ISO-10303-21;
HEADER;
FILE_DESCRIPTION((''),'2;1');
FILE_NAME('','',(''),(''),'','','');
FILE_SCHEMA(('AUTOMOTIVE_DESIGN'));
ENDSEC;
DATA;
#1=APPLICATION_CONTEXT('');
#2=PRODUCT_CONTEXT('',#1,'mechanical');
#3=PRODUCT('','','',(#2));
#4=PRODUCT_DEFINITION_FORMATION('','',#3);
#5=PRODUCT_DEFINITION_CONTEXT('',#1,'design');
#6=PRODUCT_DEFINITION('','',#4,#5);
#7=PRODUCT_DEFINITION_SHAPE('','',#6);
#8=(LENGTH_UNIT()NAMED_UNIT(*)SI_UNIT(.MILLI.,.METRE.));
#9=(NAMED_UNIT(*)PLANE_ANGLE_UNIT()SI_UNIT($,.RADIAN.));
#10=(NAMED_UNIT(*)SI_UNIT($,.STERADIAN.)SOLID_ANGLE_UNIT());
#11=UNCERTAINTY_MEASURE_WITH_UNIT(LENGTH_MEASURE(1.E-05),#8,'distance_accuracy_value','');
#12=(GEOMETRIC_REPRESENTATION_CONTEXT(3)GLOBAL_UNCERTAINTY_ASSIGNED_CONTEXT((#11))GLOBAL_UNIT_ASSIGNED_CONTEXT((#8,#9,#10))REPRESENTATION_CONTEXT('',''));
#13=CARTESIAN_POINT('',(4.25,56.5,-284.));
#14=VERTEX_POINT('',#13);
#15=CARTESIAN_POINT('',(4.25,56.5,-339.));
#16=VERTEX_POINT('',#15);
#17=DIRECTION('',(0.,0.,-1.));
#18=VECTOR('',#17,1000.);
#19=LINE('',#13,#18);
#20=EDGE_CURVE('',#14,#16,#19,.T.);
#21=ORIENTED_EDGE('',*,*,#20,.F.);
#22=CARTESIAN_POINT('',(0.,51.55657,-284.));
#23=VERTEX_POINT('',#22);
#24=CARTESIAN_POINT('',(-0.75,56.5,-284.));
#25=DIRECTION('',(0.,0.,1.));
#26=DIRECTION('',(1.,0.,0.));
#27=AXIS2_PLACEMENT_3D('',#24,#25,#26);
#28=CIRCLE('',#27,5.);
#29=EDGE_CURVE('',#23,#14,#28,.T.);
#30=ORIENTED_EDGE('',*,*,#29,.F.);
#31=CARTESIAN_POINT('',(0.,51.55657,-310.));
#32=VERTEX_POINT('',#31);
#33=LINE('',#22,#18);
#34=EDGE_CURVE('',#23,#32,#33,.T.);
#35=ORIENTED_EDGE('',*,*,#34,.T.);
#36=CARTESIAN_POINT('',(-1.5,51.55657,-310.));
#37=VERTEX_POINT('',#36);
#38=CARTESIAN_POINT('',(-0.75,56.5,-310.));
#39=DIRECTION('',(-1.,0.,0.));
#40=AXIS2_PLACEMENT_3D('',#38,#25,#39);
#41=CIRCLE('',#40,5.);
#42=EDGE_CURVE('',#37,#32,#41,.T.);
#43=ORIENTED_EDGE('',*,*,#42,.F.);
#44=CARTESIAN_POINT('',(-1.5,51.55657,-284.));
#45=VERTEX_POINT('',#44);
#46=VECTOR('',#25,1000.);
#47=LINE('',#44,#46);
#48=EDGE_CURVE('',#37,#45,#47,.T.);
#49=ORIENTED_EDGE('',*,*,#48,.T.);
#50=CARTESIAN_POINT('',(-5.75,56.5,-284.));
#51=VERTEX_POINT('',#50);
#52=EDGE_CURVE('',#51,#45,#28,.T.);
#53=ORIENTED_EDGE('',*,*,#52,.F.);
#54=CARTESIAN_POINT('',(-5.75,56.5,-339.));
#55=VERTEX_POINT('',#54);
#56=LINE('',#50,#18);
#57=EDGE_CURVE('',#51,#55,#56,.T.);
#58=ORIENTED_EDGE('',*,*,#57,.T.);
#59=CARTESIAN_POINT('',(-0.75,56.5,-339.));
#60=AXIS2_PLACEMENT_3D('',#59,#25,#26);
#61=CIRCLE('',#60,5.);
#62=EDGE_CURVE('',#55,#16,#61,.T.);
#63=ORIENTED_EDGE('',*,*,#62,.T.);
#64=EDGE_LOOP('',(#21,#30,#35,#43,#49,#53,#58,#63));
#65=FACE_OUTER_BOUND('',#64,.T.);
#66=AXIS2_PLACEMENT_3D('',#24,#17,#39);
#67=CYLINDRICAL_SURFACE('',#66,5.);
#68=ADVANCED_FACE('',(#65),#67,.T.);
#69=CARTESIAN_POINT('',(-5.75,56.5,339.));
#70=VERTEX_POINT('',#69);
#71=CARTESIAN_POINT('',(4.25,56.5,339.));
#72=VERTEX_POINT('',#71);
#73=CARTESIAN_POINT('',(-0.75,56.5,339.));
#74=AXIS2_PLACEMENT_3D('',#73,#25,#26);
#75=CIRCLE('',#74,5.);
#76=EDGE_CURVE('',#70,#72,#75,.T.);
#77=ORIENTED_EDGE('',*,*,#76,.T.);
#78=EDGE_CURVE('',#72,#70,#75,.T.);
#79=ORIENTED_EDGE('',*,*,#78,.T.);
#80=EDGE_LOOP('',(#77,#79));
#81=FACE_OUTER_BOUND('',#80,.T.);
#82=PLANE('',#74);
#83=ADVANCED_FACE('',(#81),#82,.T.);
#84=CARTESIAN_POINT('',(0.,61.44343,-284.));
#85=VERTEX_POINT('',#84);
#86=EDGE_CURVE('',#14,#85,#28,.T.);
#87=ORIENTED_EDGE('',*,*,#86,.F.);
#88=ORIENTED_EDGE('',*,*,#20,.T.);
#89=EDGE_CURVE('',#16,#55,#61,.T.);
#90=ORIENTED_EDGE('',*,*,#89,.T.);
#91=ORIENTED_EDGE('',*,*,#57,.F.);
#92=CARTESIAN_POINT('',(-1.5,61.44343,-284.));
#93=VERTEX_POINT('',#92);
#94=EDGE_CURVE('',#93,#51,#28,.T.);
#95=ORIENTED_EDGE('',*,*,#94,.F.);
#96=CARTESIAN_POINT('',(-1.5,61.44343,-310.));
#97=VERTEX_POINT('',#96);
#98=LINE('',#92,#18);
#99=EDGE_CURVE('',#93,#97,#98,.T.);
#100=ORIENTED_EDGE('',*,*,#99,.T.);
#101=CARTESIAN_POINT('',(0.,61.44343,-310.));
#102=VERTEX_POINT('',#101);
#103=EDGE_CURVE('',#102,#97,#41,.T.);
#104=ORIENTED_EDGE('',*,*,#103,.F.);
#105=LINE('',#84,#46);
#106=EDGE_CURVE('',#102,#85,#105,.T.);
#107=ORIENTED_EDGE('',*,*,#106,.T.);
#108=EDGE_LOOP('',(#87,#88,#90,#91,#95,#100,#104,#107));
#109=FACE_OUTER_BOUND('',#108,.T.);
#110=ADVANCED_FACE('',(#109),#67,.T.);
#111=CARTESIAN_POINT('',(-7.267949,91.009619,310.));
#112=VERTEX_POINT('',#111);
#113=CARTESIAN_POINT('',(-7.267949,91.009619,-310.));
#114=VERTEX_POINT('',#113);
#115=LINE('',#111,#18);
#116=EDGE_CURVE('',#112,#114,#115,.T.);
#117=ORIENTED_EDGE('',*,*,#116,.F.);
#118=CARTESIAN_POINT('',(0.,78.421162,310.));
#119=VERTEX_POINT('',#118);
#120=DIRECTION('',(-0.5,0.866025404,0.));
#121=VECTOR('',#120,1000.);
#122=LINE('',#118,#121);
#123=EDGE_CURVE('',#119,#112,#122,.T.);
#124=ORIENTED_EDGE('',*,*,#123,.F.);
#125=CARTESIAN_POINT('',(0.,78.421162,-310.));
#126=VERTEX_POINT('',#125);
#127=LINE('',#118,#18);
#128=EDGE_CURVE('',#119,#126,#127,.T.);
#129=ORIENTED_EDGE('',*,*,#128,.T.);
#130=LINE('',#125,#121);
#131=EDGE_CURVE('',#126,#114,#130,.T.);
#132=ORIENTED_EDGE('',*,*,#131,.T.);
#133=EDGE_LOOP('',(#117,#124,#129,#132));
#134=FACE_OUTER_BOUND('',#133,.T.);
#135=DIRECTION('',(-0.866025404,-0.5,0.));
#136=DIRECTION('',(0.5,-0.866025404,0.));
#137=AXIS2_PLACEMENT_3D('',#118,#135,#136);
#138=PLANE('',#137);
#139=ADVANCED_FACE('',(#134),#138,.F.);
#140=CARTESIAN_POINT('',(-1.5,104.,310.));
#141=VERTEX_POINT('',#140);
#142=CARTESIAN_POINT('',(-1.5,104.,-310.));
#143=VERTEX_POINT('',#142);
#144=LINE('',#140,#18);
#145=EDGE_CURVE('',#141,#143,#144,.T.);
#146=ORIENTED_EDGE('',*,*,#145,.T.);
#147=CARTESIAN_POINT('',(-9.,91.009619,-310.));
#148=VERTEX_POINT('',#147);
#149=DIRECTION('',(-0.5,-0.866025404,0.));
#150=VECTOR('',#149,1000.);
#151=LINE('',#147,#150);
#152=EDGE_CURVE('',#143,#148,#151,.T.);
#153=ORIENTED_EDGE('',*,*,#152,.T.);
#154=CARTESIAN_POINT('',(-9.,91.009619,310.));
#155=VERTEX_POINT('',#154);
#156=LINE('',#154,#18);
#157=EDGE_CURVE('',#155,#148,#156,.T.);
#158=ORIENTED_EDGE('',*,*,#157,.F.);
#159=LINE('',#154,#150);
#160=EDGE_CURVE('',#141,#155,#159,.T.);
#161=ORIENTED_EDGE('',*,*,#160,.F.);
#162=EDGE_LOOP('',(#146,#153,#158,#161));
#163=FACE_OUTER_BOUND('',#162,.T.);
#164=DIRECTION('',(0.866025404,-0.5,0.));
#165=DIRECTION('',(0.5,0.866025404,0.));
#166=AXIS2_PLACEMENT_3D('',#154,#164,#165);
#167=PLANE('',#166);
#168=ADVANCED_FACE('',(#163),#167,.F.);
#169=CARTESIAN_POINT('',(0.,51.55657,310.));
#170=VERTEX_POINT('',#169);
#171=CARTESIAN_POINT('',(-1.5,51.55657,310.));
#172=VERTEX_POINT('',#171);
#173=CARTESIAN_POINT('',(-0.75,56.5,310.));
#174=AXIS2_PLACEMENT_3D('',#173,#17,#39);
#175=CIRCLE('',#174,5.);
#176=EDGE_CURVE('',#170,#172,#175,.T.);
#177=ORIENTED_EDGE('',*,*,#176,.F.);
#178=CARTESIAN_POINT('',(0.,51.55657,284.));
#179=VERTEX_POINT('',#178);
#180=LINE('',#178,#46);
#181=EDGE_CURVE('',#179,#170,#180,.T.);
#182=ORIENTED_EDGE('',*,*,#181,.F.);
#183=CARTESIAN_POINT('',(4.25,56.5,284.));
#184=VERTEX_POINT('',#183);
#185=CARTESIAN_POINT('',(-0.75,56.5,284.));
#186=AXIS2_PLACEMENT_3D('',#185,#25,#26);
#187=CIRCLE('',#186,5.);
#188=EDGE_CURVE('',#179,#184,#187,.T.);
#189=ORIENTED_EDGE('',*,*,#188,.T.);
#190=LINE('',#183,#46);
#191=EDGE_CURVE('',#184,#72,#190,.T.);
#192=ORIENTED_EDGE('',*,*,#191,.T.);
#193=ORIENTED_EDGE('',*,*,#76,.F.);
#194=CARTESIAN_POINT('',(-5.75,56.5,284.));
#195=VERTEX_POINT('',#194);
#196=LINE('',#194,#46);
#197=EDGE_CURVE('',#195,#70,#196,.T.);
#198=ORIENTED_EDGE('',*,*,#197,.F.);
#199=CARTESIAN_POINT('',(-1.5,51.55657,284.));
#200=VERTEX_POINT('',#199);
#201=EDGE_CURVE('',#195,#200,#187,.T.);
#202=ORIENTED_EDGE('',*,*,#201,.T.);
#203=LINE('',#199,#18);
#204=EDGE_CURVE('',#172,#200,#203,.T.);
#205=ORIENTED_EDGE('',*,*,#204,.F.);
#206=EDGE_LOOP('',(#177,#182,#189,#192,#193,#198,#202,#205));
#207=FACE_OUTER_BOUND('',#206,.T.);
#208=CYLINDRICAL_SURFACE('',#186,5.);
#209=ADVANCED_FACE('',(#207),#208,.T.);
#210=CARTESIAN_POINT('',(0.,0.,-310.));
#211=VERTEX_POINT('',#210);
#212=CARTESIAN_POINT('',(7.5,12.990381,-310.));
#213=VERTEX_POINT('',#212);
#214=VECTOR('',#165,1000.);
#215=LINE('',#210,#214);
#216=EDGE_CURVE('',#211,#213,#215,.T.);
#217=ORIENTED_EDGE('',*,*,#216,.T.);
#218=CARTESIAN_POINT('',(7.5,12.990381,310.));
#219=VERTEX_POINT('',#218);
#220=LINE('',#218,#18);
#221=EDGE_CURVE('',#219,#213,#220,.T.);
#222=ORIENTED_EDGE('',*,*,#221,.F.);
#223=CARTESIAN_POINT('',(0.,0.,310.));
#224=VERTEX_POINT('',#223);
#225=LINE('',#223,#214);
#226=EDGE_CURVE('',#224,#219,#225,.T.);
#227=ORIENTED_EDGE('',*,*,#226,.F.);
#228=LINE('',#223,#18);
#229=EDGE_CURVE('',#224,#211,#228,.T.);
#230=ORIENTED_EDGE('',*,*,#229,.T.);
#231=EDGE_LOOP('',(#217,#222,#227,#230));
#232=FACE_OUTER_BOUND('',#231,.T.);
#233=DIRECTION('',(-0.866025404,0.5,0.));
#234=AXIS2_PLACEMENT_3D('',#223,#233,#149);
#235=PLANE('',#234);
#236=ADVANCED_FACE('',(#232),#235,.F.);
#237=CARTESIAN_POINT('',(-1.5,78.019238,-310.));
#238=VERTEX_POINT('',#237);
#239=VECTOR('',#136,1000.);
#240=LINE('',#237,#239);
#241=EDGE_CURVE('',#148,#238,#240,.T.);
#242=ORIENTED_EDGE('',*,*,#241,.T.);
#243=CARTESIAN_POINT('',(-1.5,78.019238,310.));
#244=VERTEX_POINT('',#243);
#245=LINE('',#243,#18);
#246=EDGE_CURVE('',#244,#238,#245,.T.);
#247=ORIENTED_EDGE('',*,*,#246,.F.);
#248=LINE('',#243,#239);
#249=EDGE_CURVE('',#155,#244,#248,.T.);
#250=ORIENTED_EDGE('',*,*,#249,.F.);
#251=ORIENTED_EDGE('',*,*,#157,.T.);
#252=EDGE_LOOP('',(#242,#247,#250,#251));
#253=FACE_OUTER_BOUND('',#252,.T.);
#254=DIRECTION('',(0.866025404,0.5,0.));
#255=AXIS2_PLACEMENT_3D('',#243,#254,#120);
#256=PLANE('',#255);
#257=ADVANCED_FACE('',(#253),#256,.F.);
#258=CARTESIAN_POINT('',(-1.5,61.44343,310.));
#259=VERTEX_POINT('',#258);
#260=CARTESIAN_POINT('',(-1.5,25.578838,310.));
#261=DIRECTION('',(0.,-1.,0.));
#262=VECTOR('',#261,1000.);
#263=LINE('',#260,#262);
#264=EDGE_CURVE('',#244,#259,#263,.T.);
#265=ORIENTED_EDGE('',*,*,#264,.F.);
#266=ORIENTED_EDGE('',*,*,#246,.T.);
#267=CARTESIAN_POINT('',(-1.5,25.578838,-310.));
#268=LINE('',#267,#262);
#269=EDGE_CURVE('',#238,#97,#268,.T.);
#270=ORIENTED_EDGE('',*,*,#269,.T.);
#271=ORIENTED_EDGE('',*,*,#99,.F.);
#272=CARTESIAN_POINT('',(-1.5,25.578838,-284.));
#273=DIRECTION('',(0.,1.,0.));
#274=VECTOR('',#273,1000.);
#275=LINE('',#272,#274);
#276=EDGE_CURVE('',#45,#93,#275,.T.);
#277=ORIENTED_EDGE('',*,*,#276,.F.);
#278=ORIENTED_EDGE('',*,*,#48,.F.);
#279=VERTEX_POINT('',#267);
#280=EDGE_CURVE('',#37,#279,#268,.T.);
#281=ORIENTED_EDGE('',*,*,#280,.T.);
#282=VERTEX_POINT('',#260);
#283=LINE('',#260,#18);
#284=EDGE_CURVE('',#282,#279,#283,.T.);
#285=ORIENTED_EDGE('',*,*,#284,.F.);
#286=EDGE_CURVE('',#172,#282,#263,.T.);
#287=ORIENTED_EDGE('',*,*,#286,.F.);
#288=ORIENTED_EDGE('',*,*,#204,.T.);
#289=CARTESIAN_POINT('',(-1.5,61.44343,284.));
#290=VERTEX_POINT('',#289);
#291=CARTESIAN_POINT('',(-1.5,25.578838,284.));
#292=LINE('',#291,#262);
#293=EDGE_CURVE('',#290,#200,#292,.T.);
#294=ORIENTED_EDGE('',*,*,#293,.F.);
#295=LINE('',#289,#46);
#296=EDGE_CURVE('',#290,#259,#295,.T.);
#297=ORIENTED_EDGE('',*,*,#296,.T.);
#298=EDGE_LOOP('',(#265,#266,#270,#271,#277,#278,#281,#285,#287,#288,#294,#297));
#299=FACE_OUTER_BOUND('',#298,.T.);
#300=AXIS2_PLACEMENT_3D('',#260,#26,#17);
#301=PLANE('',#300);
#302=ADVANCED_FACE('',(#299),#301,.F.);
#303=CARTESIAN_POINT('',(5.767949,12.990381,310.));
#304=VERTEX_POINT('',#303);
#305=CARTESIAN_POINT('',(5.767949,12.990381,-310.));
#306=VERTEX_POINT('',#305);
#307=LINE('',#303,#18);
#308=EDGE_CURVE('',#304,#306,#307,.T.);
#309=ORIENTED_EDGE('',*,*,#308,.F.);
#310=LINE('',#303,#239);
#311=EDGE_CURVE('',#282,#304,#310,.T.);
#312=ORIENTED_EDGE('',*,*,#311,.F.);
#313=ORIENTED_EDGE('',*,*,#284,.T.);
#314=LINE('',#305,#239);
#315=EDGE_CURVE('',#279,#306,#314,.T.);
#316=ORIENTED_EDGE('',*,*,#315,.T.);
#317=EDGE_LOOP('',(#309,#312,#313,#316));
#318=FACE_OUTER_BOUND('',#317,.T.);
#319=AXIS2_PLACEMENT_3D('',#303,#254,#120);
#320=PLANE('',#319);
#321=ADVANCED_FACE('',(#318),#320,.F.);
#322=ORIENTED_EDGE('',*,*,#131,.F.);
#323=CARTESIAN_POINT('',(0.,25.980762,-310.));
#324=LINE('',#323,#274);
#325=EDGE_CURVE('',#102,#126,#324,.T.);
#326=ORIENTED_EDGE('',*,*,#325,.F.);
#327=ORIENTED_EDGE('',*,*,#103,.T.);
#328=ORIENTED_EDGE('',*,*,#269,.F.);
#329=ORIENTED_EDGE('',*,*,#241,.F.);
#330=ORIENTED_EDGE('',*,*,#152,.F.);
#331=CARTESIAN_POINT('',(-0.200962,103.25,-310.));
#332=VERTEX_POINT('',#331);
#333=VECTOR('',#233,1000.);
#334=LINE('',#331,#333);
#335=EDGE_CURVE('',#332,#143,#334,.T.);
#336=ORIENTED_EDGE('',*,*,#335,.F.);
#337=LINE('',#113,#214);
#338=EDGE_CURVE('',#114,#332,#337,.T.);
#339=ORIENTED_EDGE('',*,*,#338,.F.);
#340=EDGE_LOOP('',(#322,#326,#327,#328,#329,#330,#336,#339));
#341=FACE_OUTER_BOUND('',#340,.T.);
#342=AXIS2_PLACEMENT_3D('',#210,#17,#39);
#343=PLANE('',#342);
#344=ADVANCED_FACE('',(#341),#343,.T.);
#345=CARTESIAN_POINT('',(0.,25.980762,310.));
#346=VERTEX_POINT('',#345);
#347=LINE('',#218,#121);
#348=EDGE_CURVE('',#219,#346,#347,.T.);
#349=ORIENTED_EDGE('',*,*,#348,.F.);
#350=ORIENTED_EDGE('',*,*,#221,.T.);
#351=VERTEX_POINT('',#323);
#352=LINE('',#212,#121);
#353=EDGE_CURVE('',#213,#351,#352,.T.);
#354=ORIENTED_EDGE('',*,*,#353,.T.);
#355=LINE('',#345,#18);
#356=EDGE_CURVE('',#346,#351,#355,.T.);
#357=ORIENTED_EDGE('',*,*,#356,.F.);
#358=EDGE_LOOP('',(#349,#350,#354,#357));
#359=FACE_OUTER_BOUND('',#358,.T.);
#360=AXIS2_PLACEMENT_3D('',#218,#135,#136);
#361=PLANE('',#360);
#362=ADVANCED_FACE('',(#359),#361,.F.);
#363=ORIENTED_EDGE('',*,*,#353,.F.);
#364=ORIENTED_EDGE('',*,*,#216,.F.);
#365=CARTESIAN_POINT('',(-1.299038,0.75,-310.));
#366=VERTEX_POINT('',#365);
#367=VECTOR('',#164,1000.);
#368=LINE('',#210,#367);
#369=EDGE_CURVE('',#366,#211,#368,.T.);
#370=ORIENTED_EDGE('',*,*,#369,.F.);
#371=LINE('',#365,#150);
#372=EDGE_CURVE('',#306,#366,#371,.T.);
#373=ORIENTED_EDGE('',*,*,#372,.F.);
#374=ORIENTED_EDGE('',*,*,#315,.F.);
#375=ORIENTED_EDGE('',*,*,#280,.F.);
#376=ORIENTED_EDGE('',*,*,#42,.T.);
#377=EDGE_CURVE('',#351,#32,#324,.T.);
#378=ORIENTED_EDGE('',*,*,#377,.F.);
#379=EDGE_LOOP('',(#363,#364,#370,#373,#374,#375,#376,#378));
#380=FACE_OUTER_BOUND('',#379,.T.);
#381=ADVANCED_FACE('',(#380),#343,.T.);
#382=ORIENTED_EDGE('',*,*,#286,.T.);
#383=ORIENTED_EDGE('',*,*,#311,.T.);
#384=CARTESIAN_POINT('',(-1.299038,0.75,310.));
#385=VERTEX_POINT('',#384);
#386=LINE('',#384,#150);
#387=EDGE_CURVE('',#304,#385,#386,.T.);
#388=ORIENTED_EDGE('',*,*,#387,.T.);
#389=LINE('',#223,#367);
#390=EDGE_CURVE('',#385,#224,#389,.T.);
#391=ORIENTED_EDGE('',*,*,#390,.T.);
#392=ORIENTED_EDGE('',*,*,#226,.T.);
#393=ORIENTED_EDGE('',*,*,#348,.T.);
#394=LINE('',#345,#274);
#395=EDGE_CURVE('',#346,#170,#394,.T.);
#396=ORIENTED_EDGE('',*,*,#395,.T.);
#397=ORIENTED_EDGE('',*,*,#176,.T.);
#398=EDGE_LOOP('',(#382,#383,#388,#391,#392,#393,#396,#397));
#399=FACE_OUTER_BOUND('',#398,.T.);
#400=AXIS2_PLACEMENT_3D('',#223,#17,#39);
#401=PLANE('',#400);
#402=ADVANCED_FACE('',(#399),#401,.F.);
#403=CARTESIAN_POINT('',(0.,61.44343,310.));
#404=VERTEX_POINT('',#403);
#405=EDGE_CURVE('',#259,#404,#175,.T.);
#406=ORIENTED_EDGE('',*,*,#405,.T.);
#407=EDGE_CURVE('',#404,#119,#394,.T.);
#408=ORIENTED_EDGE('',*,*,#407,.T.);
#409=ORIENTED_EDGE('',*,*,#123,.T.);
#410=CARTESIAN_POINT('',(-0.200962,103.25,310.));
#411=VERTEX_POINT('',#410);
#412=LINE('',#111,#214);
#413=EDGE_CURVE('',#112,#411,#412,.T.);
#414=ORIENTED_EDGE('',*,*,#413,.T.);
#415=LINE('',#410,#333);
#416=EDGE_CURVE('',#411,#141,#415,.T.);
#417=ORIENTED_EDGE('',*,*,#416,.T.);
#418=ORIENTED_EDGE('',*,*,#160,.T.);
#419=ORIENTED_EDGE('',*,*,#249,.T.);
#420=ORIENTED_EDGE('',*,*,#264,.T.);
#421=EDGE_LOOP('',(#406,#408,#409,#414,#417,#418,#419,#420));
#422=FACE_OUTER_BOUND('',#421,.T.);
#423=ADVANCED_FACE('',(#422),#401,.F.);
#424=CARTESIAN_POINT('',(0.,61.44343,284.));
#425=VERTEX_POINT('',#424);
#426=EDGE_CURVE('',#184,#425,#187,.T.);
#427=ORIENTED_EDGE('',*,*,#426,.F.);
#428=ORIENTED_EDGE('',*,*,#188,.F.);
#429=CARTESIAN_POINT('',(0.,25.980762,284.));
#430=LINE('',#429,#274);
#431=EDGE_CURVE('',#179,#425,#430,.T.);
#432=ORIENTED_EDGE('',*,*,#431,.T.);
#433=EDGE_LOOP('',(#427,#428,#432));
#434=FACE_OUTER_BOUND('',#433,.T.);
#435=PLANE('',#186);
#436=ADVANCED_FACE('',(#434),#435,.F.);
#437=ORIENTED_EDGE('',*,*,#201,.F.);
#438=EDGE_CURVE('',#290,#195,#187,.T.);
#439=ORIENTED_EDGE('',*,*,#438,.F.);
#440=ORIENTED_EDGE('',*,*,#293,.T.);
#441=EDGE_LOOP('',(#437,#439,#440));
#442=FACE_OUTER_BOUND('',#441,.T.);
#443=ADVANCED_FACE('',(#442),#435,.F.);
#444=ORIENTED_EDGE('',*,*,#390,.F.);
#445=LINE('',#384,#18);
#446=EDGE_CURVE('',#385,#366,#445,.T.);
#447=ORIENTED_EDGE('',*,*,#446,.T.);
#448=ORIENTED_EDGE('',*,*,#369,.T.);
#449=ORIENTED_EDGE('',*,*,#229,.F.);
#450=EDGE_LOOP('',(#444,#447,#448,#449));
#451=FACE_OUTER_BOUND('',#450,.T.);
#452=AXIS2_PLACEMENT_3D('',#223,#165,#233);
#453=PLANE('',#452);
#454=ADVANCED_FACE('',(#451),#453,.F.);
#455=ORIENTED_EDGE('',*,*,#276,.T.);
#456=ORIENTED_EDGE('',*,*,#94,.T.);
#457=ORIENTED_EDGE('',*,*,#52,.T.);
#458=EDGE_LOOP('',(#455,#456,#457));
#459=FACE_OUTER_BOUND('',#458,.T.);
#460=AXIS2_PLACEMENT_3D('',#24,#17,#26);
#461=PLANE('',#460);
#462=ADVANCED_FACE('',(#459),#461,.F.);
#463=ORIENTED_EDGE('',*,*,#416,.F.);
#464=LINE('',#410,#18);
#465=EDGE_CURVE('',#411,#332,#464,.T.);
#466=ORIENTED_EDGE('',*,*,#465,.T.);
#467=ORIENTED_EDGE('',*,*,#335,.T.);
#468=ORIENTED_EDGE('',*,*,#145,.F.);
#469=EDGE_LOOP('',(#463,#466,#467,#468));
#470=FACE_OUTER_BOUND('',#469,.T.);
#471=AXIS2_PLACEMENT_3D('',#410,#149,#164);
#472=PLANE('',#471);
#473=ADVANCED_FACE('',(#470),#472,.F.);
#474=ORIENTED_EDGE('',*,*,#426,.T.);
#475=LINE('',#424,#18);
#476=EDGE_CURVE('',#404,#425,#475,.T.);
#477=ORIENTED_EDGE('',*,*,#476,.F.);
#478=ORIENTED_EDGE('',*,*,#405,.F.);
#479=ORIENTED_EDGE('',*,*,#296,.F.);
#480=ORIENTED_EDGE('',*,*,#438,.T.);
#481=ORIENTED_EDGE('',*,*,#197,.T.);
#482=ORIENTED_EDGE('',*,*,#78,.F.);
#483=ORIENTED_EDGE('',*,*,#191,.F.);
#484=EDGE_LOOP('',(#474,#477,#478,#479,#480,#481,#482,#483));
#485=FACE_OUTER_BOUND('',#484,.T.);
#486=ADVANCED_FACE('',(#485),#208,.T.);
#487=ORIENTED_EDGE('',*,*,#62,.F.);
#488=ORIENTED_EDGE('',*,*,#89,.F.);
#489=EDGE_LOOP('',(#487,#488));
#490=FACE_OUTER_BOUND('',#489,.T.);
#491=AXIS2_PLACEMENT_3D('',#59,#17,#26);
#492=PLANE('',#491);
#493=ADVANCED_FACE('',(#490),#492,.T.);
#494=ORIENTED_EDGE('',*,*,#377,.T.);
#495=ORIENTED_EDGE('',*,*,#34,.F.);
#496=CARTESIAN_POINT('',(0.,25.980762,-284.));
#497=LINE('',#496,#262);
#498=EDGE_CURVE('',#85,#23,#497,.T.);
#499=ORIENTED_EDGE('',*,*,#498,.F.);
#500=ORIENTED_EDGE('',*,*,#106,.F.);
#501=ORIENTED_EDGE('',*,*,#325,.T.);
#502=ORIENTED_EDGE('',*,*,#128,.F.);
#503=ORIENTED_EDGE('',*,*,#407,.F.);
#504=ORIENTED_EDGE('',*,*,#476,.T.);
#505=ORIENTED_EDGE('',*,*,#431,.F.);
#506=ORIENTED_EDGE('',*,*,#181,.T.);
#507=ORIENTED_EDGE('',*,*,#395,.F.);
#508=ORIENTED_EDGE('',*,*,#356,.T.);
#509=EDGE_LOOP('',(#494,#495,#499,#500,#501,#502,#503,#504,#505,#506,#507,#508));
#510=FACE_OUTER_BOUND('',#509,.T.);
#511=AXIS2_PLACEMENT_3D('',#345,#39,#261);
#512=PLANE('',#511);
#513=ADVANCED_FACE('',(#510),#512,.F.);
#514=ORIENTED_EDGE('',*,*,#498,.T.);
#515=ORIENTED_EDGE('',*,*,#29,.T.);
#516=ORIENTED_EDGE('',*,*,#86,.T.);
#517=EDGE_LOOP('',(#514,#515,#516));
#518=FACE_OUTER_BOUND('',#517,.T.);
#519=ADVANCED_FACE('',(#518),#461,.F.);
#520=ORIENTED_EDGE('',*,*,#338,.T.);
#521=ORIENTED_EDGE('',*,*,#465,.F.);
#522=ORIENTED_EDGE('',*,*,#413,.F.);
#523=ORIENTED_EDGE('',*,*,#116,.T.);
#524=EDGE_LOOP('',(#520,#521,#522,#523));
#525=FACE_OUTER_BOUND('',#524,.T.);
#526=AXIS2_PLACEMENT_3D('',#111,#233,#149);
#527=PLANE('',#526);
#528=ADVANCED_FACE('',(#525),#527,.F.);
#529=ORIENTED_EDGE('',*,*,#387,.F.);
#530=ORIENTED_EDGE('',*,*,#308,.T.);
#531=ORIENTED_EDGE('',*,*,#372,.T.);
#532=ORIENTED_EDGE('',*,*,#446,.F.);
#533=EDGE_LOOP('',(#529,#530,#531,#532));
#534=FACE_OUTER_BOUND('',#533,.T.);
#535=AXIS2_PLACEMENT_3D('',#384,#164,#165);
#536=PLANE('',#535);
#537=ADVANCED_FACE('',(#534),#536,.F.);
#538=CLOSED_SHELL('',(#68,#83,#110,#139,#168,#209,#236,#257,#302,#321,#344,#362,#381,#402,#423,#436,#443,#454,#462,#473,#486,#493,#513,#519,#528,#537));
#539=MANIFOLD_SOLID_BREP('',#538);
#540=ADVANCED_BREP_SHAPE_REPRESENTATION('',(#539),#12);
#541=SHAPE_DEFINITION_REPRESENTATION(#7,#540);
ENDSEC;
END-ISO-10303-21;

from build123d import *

# Parameters (mm, degrees)
BOSS_EXTRUDE1_DEPTH = 310
BOSS_EXTRUDE2_START = -26
SKETCH2_R           = 5
BOSS_EXTRUDE2_DEPTH = 55


with BuildPart() as part:
    # Sketch1 → Boss-Extrude1 (new, symmetric)
    with BuildSketch(Plane.XY):
        Polygon((0, 0), (7.5, 12.990381057), (0, 25.980762114), (0, 78.421161675), (-7.267949192, 91.009618943), (-0.200961894, 103.25), (-1.5, 104), (-9, 91.009618943), (-1.5, 78.019237886), (-1.5, 25.578838325), (5.767949192, 12.990381057), (-1.299038106, 0.75), align=None)
    extrude(amount=BOSS_EXTRUDE1_DEPTH, both=True)

    # Sketch2 → Boss-Extrude2 (add)
    with BuildSketch(Plane.XY.offset(310).offset(BOSS_EXTRUDE2_START)):
        with Locations((-0.75, 56.5)):
            Circle(SKETCH2_R)
    boss_extrude2 = extrude(amount=BOSS_EXTRUDE2_DEPTH)

    # Mirror1: Boss-Extrude2 across plane
    add(boss_extrude2.mirror(Plane.XY))


solid = part.part
